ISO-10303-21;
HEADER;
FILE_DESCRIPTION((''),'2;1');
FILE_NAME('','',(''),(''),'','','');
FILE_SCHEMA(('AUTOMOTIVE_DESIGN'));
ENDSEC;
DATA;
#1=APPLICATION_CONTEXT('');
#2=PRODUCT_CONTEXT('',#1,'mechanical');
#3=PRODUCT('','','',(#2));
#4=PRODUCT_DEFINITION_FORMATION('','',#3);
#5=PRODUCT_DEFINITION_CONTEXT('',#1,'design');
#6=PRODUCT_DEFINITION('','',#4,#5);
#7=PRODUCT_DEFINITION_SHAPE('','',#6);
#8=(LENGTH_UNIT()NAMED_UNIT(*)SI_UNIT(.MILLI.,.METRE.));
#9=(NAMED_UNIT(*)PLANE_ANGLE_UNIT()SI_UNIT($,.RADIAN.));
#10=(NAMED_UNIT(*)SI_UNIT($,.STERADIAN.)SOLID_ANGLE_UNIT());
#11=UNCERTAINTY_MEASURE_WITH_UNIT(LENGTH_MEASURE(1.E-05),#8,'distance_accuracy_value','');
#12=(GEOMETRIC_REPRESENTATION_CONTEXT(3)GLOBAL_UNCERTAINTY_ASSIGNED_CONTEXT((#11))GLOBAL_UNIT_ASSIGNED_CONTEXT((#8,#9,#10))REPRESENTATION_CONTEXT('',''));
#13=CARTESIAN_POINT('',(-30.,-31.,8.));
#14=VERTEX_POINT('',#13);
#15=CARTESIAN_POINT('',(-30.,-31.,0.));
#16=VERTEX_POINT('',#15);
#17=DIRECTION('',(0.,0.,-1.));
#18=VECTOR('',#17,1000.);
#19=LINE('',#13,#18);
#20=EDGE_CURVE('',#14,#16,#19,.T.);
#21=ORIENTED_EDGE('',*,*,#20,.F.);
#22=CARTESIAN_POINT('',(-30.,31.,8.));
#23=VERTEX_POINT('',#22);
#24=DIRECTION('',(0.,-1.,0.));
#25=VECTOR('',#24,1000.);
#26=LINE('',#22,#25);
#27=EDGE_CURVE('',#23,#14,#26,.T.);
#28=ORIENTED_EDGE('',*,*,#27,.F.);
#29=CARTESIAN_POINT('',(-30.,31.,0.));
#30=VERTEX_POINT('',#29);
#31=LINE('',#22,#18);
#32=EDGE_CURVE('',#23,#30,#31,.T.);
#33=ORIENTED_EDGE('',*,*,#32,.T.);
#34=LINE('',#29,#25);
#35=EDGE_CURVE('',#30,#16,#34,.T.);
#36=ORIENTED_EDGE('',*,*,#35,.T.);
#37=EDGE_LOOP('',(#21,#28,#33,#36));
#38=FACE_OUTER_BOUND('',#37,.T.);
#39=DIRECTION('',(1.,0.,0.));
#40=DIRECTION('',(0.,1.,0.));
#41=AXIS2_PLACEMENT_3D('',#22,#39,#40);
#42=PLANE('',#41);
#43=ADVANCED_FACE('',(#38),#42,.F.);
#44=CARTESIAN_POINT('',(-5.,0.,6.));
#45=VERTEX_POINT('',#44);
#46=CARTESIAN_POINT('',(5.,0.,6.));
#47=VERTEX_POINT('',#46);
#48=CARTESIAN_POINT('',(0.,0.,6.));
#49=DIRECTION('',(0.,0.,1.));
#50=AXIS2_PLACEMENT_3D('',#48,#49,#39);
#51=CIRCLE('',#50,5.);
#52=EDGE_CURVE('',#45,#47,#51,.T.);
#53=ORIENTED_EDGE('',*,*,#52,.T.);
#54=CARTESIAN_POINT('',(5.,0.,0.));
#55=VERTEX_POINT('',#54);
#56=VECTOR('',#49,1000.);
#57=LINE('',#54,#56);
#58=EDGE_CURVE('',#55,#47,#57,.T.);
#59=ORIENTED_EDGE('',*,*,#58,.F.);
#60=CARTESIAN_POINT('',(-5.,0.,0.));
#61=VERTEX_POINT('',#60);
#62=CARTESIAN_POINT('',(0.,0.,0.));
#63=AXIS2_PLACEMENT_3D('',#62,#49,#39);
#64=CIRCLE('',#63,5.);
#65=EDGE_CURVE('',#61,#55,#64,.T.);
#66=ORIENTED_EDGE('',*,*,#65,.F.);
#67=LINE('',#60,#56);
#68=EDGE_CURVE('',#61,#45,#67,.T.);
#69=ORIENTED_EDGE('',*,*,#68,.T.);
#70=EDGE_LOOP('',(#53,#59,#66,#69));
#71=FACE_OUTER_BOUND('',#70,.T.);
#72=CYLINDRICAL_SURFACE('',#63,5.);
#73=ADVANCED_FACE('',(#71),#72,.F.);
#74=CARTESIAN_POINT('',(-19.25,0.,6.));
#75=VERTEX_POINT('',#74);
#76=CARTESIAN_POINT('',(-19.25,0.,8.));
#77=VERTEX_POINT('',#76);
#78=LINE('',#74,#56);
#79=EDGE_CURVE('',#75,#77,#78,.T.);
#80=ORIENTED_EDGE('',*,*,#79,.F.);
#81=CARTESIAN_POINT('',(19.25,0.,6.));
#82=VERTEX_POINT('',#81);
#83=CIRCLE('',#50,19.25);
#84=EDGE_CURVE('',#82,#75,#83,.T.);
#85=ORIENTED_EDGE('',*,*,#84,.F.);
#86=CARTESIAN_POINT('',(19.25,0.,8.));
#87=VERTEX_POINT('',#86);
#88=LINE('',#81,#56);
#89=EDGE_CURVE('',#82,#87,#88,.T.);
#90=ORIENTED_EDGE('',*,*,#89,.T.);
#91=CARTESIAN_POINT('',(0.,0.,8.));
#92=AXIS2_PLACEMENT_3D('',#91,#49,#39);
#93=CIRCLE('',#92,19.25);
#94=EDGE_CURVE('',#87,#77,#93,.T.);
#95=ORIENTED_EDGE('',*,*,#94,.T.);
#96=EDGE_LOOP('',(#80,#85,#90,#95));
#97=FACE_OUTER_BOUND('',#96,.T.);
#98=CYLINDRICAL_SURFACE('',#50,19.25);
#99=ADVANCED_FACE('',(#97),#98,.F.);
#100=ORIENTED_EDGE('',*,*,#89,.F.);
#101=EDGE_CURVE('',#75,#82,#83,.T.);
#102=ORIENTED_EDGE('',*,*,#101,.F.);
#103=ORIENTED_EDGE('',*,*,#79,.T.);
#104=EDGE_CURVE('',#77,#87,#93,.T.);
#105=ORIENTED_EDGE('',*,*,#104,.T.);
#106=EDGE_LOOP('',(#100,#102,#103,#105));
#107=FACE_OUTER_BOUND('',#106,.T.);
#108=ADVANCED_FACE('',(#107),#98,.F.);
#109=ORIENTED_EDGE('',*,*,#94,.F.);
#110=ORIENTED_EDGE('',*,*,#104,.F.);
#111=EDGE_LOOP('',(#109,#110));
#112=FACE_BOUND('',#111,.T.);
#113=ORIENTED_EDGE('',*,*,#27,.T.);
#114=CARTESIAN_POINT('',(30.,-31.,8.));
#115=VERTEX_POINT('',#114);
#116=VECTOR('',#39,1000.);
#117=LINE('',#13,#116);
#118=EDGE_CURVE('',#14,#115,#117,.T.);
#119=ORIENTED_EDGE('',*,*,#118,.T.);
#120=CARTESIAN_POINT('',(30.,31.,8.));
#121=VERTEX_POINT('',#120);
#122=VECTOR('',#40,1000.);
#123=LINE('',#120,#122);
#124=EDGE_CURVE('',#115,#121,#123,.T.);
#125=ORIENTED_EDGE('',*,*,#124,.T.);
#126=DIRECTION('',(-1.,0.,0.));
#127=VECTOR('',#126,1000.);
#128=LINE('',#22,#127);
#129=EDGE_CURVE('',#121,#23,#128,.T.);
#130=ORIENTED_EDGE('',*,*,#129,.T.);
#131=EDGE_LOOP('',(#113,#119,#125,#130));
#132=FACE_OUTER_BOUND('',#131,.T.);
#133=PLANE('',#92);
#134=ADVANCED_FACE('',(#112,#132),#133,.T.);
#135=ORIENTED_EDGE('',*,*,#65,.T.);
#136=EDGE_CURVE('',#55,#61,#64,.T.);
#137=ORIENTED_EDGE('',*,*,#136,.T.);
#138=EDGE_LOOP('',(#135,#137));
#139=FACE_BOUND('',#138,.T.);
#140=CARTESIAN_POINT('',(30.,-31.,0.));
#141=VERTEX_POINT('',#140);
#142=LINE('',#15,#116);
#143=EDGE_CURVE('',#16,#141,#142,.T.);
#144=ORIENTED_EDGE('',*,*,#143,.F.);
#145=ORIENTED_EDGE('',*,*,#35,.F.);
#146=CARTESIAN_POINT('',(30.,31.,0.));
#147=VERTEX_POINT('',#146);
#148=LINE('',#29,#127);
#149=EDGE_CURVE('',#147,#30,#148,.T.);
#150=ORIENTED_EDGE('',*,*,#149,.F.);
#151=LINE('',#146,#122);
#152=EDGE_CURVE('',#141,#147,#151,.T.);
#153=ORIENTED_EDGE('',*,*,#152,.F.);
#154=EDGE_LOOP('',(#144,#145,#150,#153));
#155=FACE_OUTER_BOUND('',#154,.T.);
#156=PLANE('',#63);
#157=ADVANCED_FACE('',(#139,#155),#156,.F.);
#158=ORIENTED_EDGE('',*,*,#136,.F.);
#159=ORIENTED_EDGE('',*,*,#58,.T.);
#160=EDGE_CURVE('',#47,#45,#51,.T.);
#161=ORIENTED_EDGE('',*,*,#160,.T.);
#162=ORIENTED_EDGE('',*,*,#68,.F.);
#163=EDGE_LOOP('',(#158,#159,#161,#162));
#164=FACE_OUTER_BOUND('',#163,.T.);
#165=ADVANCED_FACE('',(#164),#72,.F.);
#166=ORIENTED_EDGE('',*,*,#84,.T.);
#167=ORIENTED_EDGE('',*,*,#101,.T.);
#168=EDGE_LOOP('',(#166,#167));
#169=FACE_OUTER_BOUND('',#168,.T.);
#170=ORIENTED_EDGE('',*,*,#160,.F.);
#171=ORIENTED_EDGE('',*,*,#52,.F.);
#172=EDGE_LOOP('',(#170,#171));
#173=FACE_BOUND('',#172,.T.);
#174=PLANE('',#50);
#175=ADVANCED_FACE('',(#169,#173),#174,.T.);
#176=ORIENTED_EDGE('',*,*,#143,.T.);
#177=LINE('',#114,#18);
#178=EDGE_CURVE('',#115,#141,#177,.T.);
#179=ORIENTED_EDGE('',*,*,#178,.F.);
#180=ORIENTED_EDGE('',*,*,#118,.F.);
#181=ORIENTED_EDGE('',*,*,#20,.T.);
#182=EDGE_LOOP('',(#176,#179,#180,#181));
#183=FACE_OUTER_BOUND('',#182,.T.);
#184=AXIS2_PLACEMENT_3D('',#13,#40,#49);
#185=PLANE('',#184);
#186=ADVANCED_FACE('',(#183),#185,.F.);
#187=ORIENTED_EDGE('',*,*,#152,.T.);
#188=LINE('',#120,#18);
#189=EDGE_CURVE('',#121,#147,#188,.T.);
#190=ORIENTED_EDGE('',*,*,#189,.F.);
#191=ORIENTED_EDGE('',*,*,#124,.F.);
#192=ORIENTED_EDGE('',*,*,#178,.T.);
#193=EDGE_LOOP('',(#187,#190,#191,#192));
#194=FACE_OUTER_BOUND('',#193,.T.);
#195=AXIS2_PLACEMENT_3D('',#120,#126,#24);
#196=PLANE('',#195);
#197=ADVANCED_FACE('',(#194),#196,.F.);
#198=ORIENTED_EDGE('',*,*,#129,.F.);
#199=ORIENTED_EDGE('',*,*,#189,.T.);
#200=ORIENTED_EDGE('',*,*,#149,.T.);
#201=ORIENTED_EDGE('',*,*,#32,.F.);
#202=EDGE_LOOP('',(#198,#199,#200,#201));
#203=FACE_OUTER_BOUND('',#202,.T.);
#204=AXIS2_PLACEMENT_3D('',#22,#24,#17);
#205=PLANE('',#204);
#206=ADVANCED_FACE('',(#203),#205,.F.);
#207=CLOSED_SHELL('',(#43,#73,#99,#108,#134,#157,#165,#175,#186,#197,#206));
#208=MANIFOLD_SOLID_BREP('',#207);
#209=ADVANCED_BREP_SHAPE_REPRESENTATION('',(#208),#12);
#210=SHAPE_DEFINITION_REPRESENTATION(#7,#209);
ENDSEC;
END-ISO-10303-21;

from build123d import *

# Parameters (mm, degrees)
SKETCH1_W           = 60
SKETCH1_H           = 62
BOSS_EXTRUDE1_DEPTH = 8
SKETCH3_R           = 19.25
CUT_EXTRUDE1_DEPTH  = 2
SKETCH4_R           = 5
CUT_EXTRUDE2_DEPTH  = 44.554563481


with BuildPart() as part:
    # Sketch1 → Boss-Extrude1 (new body)
    with BuildSketch(Plane.XY):
        Rectangle(SKETCH1_W, SKETCH1_H)
    extrude(amount=BOSS_EXTRUDE1_DEPTH)

    # Sketch3 → Cut-Extrude1 (cut)
    with BuildSketch(Plane.XY.offset(8)):
        Circle(SKETCH3_R)
    extrude(amount=-CUT_EXTRUDE1_DEPTH, mode=Mode.SUBTRACT)

    # Sketch4 → Cut-Extrude2 (cut, through all)
    with BuildSketch(Plane.XY.offset(6)):
        Circle(SKETCH4_R)
    extrude(amount=-CUT_EXTRUDE2_DEPTH, mode=Mode.SUBTRACT)


solid = part.part
